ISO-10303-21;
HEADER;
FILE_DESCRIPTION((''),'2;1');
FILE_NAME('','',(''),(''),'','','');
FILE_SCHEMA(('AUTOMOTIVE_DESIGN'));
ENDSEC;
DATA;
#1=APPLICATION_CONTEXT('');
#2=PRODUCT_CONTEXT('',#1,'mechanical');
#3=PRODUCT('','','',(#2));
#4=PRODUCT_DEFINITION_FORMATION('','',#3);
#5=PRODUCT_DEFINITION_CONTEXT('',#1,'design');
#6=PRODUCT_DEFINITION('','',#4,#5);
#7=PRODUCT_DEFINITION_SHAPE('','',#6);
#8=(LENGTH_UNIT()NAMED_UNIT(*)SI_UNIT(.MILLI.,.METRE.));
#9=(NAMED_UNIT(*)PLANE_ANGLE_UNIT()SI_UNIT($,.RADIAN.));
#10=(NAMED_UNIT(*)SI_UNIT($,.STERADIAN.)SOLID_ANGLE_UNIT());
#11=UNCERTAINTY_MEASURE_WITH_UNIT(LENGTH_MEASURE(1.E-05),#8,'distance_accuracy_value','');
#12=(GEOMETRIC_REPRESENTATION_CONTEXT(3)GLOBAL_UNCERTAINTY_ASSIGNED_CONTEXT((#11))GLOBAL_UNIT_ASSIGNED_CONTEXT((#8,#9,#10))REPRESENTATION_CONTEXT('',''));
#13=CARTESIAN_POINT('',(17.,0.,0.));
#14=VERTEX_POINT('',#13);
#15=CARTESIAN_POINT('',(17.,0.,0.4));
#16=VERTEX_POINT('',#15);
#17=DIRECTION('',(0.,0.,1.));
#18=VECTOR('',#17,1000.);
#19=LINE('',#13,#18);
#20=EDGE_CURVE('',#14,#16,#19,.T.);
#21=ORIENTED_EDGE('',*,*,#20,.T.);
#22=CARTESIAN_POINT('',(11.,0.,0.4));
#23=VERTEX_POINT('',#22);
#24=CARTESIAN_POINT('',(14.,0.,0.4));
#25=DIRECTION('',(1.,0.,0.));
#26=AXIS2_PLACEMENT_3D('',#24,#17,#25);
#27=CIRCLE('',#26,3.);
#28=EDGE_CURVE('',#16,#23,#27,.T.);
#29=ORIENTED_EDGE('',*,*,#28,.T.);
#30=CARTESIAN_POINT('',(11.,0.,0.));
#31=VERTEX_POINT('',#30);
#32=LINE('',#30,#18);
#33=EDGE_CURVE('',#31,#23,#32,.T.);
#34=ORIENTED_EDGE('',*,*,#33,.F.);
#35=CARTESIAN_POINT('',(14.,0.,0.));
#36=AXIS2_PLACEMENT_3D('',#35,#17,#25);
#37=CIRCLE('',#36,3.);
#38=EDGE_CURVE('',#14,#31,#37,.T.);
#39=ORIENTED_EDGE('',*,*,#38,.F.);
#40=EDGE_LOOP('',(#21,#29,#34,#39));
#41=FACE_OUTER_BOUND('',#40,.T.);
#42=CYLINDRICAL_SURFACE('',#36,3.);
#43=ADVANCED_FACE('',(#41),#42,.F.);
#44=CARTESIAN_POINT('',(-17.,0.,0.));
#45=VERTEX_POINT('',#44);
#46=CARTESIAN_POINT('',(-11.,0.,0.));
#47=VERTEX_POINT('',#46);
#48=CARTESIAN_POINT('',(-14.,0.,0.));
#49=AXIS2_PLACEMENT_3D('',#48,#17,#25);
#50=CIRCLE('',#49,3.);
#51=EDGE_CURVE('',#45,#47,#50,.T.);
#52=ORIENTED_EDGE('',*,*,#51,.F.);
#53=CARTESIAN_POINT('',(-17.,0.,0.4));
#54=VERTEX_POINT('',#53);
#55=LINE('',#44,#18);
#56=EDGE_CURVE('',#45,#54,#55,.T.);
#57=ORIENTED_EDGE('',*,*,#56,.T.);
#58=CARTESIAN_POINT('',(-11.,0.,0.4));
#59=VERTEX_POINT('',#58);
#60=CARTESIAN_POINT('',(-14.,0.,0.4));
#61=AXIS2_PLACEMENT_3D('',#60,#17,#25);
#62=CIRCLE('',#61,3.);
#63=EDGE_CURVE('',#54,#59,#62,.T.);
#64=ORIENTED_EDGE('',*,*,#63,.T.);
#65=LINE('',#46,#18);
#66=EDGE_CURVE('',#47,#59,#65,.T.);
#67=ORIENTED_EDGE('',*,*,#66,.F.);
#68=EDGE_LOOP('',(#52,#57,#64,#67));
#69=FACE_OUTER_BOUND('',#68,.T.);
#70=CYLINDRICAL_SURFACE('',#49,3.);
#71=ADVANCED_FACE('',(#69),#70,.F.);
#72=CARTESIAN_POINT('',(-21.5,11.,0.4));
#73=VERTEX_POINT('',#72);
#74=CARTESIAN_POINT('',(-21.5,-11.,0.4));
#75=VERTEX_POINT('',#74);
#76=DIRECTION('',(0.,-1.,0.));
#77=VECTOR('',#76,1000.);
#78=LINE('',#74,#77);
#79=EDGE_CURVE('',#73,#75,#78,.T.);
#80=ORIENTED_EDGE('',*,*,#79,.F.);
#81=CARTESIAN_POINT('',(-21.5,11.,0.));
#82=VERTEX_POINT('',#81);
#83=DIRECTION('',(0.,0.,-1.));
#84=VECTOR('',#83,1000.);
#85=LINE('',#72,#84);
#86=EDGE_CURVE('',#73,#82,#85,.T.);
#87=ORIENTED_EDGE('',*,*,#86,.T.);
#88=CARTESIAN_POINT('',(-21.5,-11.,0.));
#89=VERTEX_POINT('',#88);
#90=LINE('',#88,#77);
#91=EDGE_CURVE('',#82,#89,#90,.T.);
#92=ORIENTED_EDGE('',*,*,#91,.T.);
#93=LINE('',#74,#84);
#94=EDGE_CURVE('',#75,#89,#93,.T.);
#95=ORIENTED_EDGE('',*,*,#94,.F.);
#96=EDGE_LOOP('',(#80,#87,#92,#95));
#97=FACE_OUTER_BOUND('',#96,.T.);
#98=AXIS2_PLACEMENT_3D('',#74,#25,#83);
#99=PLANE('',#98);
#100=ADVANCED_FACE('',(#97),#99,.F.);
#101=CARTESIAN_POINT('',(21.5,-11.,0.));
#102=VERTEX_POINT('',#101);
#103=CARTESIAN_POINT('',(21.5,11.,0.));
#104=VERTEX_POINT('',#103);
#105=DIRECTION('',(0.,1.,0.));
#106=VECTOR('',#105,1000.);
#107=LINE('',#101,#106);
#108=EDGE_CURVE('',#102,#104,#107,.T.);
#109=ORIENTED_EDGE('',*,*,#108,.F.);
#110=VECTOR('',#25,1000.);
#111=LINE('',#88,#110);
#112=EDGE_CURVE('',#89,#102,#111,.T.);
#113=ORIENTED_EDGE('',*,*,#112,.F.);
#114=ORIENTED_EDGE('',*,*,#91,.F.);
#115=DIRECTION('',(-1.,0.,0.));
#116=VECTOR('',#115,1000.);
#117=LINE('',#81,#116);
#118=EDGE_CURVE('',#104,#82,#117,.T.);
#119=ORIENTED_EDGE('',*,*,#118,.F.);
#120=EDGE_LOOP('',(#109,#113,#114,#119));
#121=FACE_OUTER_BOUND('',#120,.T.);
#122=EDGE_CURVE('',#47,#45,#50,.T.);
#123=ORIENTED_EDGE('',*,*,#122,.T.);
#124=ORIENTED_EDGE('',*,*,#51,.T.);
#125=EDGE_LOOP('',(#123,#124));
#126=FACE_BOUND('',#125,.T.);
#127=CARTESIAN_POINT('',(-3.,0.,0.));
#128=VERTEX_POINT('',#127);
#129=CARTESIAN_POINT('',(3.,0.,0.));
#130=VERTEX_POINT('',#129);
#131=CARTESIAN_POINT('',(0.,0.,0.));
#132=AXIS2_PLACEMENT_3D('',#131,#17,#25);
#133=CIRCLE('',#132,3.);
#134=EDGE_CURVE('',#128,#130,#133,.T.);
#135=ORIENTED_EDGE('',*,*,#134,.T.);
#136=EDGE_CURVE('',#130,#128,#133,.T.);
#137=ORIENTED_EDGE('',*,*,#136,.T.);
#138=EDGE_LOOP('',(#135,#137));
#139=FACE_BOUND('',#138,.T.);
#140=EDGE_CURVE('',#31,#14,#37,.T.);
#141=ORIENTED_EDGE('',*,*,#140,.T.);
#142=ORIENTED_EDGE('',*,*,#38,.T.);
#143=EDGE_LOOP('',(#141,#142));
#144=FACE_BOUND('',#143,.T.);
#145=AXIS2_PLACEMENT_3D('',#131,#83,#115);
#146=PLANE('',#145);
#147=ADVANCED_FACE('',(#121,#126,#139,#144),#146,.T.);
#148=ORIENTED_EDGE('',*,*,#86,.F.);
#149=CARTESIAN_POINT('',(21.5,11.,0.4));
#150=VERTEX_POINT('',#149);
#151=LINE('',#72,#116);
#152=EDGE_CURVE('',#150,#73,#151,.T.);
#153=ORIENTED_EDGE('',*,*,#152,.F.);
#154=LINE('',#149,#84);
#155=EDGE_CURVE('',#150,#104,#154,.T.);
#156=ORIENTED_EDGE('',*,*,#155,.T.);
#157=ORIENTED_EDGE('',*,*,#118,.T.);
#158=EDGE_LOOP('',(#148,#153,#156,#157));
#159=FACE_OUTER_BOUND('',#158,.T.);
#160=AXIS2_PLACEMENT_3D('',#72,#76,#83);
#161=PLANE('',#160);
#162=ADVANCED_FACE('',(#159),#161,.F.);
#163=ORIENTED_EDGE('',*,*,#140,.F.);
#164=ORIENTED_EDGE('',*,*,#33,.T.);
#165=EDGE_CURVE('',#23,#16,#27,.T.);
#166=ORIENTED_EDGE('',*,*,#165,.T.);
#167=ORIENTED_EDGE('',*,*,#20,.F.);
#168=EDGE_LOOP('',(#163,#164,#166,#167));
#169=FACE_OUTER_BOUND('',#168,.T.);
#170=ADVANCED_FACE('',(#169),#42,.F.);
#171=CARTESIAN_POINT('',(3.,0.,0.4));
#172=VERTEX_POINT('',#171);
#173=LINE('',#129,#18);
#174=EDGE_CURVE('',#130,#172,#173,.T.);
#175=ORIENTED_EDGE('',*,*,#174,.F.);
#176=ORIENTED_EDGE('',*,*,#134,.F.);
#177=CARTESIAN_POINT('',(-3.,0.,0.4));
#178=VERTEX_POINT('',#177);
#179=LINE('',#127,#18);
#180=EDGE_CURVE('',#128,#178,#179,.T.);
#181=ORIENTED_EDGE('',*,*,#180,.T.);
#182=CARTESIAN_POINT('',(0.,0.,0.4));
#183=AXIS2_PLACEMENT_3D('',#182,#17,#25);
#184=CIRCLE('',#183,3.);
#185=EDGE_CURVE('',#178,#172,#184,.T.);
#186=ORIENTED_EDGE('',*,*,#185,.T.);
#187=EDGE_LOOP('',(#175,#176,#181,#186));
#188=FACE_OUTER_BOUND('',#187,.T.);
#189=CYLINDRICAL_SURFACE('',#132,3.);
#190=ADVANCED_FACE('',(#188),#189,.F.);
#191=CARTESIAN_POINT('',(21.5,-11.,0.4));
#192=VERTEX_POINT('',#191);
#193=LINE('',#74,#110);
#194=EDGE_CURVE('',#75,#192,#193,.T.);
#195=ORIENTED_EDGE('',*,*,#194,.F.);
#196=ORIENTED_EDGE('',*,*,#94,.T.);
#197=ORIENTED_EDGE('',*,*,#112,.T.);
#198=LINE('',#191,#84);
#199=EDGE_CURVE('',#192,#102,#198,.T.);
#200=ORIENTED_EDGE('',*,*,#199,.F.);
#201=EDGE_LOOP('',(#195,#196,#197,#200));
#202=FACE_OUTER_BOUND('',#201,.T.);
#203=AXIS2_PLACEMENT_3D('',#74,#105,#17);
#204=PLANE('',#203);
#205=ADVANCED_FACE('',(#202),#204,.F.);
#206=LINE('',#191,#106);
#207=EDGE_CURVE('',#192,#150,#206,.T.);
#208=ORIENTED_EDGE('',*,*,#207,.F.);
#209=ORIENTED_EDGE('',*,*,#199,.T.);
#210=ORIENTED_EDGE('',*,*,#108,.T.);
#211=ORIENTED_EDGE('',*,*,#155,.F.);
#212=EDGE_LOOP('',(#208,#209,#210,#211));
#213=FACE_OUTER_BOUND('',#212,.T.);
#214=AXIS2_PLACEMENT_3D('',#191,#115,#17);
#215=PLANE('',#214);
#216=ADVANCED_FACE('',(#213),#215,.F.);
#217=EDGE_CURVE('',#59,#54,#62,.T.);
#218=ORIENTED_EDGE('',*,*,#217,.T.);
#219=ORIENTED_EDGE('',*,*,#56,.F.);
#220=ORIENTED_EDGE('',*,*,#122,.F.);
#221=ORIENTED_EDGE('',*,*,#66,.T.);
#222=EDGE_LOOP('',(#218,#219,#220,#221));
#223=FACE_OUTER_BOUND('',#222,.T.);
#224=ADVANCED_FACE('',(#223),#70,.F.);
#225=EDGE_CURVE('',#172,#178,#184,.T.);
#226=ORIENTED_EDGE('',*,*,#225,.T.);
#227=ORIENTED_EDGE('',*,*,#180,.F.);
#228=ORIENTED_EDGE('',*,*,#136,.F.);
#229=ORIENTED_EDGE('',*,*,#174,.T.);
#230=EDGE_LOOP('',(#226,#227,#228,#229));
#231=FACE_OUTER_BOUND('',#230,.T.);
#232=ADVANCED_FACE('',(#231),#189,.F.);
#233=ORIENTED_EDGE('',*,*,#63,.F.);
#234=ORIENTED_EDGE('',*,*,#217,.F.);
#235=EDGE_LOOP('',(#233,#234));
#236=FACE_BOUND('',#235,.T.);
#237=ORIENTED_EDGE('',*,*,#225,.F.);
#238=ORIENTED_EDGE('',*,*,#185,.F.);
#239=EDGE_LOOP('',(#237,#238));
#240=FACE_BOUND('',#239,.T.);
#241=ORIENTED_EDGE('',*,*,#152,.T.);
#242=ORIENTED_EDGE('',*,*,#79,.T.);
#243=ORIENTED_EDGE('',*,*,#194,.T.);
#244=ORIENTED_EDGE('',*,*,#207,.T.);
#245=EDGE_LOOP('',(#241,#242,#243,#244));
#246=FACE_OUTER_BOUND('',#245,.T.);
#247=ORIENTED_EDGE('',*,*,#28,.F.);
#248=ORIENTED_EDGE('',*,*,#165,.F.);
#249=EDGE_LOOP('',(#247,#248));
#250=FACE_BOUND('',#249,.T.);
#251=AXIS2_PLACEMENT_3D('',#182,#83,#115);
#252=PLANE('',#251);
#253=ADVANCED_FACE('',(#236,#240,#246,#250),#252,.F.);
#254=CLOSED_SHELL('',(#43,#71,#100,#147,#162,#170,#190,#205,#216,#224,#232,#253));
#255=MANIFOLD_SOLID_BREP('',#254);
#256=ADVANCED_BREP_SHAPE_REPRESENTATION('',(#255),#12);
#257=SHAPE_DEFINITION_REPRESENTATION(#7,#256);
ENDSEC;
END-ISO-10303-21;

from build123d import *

# Parameters (mm, degrees)
SKETCH_1_W          = 43
SKETCH_1_H          = 22
EXTRUDE_1_DEPTH     = 0.4
SKETCH_2_R          = 3
CUT_EXTRUDE_1_DEPTH = 0.4


with BuildPart() as part:
    # 草图1 → 凸台-拉伸1 (new body)
    with BuildSketch(Plane.XY):
        Rectangle(SKETCH_1_W, SKETCH_1_H)
    extrude(amount=EXTRUDE_1_DEPTH)

    # 草图2 → 切除-拉伸1 (cut)
    with BuildSketch(Plane.XY.offset(0.4)):
        Circle(SKETCH_2_R)
        with Locations((-14, 0)):
            Circle(SKETCH_2_R)
        with Locations((14, 0)):
            Circle(SKETCH_2_R)
    extrude(amount=-CUT_EXTRUDE_1_DEPTH, mode=Mode.SUBTRACT)


solid = part.part
